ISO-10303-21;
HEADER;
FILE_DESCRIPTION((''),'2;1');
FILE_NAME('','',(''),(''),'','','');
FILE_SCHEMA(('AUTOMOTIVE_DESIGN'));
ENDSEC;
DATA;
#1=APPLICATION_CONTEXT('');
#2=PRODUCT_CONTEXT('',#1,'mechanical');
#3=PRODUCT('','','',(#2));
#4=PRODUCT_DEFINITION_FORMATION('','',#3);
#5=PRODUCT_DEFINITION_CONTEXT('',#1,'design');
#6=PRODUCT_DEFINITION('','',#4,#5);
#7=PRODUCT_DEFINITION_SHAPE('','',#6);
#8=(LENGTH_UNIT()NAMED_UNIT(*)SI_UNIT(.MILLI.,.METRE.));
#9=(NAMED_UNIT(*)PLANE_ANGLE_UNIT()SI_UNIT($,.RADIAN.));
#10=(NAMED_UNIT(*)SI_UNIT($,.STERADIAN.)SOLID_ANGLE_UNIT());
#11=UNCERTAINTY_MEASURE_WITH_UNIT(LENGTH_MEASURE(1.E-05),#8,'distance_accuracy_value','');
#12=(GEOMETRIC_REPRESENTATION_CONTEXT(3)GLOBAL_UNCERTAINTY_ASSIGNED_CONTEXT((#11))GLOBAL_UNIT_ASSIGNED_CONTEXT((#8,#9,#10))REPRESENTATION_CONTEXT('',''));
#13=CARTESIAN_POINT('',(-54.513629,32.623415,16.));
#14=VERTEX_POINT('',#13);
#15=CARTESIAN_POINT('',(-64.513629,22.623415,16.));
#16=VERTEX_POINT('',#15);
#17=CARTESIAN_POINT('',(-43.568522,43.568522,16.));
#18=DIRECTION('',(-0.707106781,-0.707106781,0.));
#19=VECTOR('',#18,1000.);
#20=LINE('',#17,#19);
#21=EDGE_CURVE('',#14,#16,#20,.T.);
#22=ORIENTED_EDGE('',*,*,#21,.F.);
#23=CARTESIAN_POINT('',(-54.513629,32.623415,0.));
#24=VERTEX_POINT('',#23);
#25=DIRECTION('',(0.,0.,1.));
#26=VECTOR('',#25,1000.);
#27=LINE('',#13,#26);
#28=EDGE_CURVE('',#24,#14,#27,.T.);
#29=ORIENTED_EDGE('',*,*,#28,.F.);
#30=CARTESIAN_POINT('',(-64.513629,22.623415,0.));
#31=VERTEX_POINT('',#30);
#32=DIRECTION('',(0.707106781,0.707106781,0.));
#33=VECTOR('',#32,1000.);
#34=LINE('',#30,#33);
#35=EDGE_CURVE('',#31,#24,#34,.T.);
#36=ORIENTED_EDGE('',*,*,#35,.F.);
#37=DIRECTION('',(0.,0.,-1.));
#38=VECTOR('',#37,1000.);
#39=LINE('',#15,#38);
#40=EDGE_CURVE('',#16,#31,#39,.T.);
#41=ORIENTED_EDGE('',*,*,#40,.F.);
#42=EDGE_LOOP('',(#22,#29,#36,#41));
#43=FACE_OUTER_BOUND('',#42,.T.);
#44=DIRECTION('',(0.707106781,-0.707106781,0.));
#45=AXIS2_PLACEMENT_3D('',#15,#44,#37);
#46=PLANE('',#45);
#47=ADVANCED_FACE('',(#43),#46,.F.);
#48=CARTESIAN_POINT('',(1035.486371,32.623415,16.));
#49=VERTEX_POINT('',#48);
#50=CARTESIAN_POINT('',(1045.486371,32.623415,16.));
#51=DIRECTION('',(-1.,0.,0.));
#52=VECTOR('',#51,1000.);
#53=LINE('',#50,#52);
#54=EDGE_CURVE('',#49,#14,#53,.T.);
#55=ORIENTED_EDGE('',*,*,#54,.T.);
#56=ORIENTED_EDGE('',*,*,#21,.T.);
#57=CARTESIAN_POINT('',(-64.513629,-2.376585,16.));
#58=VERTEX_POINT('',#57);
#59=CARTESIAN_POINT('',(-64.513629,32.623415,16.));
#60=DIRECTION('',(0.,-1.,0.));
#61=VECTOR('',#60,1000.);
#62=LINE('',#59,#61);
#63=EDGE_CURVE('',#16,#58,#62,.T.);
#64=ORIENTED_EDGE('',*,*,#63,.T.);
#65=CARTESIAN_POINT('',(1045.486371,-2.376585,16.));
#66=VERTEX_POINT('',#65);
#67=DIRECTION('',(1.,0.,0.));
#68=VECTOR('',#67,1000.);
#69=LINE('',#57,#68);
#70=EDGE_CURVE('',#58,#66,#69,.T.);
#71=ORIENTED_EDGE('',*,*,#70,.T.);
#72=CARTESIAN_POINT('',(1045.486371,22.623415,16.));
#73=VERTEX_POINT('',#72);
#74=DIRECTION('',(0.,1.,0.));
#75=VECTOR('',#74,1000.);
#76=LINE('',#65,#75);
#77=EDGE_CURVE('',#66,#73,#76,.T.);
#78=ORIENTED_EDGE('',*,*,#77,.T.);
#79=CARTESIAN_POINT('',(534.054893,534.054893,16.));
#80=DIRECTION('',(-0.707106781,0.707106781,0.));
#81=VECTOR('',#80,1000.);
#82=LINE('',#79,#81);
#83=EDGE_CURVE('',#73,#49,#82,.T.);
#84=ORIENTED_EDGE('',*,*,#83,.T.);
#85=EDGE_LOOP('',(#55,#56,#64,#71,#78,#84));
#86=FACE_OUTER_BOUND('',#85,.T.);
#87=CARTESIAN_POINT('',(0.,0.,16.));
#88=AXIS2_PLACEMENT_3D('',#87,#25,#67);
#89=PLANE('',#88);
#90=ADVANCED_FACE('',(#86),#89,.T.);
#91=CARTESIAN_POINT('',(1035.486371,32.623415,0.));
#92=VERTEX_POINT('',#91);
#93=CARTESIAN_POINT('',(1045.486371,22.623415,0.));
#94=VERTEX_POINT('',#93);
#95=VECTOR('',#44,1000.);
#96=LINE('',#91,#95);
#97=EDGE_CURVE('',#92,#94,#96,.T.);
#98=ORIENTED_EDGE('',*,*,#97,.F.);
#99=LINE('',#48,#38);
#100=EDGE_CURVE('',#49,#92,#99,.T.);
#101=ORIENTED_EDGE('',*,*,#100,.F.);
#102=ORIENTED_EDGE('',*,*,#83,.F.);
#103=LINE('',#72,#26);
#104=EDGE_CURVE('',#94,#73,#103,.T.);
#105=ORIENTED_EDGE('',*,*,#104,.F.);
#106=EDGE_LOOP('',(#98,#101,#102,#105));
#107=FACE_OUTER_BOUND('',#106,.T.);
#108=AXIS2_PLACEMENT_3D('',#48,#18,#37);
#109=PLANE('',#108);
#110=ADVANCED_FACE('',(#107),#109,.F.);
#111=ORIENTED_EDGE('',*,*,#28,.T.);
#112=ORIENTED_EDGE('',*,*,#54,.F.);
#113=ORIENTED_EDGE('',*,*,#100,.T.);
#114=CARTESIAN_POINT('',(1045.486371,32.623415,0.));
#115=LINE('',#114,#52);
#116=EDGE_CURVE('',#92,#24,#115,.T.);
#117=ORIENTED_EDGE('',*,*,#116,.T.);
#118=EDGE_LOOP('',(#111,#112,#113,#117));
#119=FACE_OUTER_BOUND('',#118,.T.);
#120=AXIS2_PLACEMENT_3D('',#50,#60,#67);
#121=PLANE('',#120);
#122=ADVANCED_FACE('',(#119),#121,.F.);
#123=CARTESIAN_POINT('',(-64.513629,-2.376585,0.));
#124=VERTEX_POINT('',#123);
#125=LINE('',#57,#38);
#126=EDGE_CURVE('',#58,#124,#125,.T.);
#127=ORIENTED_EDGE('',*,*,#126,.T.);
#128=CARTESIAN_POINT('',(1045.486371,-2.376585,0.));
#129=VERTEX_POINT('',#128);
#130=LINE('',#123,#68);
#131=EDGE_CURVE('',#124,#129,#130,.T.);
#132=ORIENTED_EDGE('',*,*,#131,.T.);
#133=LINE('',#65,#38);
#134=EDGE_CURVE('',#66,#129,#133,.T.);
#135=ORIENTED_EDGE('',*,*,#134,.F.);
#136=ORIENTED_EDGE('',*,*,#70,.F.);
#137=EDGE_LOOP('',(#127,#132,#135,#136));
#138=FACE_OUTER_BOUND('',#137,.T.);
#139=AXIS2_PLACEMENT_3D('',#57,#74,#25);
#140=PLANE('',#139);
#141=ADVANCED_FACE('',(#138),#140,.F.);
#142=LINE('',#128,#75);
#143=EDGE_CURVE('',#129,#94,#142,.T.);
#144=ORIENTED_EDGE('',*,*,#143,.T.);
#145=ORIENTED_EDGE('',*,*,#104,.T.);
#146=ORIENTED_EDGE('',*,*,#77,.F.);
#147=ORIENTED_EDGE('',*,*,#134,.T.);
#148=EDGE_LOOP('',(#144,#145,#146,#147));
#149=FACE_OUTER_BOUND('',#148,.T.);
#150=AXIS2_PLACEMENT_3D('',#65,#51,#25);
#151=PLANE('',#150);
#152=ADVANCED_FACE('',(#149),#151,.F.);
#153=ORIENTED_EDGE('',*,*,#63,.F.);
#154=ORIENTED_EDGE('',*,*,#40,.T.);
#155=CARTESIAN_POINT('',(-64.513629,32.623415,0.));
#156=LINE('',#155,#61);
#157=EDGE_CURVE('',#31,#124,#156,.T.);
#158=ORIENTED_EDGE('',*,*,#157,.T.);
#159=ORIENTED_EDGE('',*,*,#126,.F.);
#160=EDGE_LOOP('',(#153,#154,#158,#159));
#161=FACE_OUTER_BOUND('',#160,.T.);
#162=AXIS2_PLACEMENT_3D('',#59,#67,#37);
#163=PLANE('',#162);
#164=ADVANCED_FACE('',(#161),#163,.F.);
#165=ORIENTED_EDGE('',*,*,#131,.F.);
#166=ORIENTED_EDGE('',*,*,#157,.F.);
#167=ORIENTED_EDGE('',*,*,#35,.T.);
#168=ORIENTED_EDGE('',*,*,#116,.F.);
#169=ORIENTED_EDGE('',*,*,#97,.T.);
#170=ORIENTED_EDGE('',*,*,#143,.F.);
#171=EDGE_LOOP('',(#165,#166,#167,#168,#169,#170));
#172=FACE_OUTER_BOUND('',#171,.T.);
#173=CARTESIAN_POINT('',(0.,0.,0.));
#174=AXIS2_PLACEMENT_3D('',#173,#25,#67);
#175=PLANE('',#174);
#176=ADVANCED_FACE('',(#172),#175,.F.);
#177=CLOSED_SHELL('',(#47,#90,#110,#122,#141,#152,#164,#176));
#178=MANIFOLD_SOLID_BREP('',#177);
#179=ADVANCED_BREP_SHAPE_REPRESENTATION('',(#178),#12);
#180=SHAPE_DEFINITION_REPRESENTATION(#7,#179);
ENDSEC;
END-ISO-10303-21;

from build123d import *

# Parameters (mm, degrees)
SKETCH1_W           = 1110
SKETCH1_H           = 35
BOSS_EXTRUDE1_DEPTH = 16
CHAMFER1_SIZE       = 10


with BuildPart() as part:
    # Sketch1 → Boss-Extrude1 (new body)
    with BuildSketch(Plane.XY):
        with Locations((490.486370787, 15.12341466)):
            Rectangle(SKETCH1_W, SKETCH1_H)
    extrude(amount=BOSS_EXTRUDE1_DEPTH)

    # Chamfer1
    chamfer1_edges = [part.edges().sort_by_distance(p)[0] for p in [
        (1045.486370787, 32.62341466, 8),
        (-64.513629213, 32.62341466, 8),
    ]]
    chamfer(chamfer1_edges, length=CHAMFER1_SIZE)


solid = part.part
